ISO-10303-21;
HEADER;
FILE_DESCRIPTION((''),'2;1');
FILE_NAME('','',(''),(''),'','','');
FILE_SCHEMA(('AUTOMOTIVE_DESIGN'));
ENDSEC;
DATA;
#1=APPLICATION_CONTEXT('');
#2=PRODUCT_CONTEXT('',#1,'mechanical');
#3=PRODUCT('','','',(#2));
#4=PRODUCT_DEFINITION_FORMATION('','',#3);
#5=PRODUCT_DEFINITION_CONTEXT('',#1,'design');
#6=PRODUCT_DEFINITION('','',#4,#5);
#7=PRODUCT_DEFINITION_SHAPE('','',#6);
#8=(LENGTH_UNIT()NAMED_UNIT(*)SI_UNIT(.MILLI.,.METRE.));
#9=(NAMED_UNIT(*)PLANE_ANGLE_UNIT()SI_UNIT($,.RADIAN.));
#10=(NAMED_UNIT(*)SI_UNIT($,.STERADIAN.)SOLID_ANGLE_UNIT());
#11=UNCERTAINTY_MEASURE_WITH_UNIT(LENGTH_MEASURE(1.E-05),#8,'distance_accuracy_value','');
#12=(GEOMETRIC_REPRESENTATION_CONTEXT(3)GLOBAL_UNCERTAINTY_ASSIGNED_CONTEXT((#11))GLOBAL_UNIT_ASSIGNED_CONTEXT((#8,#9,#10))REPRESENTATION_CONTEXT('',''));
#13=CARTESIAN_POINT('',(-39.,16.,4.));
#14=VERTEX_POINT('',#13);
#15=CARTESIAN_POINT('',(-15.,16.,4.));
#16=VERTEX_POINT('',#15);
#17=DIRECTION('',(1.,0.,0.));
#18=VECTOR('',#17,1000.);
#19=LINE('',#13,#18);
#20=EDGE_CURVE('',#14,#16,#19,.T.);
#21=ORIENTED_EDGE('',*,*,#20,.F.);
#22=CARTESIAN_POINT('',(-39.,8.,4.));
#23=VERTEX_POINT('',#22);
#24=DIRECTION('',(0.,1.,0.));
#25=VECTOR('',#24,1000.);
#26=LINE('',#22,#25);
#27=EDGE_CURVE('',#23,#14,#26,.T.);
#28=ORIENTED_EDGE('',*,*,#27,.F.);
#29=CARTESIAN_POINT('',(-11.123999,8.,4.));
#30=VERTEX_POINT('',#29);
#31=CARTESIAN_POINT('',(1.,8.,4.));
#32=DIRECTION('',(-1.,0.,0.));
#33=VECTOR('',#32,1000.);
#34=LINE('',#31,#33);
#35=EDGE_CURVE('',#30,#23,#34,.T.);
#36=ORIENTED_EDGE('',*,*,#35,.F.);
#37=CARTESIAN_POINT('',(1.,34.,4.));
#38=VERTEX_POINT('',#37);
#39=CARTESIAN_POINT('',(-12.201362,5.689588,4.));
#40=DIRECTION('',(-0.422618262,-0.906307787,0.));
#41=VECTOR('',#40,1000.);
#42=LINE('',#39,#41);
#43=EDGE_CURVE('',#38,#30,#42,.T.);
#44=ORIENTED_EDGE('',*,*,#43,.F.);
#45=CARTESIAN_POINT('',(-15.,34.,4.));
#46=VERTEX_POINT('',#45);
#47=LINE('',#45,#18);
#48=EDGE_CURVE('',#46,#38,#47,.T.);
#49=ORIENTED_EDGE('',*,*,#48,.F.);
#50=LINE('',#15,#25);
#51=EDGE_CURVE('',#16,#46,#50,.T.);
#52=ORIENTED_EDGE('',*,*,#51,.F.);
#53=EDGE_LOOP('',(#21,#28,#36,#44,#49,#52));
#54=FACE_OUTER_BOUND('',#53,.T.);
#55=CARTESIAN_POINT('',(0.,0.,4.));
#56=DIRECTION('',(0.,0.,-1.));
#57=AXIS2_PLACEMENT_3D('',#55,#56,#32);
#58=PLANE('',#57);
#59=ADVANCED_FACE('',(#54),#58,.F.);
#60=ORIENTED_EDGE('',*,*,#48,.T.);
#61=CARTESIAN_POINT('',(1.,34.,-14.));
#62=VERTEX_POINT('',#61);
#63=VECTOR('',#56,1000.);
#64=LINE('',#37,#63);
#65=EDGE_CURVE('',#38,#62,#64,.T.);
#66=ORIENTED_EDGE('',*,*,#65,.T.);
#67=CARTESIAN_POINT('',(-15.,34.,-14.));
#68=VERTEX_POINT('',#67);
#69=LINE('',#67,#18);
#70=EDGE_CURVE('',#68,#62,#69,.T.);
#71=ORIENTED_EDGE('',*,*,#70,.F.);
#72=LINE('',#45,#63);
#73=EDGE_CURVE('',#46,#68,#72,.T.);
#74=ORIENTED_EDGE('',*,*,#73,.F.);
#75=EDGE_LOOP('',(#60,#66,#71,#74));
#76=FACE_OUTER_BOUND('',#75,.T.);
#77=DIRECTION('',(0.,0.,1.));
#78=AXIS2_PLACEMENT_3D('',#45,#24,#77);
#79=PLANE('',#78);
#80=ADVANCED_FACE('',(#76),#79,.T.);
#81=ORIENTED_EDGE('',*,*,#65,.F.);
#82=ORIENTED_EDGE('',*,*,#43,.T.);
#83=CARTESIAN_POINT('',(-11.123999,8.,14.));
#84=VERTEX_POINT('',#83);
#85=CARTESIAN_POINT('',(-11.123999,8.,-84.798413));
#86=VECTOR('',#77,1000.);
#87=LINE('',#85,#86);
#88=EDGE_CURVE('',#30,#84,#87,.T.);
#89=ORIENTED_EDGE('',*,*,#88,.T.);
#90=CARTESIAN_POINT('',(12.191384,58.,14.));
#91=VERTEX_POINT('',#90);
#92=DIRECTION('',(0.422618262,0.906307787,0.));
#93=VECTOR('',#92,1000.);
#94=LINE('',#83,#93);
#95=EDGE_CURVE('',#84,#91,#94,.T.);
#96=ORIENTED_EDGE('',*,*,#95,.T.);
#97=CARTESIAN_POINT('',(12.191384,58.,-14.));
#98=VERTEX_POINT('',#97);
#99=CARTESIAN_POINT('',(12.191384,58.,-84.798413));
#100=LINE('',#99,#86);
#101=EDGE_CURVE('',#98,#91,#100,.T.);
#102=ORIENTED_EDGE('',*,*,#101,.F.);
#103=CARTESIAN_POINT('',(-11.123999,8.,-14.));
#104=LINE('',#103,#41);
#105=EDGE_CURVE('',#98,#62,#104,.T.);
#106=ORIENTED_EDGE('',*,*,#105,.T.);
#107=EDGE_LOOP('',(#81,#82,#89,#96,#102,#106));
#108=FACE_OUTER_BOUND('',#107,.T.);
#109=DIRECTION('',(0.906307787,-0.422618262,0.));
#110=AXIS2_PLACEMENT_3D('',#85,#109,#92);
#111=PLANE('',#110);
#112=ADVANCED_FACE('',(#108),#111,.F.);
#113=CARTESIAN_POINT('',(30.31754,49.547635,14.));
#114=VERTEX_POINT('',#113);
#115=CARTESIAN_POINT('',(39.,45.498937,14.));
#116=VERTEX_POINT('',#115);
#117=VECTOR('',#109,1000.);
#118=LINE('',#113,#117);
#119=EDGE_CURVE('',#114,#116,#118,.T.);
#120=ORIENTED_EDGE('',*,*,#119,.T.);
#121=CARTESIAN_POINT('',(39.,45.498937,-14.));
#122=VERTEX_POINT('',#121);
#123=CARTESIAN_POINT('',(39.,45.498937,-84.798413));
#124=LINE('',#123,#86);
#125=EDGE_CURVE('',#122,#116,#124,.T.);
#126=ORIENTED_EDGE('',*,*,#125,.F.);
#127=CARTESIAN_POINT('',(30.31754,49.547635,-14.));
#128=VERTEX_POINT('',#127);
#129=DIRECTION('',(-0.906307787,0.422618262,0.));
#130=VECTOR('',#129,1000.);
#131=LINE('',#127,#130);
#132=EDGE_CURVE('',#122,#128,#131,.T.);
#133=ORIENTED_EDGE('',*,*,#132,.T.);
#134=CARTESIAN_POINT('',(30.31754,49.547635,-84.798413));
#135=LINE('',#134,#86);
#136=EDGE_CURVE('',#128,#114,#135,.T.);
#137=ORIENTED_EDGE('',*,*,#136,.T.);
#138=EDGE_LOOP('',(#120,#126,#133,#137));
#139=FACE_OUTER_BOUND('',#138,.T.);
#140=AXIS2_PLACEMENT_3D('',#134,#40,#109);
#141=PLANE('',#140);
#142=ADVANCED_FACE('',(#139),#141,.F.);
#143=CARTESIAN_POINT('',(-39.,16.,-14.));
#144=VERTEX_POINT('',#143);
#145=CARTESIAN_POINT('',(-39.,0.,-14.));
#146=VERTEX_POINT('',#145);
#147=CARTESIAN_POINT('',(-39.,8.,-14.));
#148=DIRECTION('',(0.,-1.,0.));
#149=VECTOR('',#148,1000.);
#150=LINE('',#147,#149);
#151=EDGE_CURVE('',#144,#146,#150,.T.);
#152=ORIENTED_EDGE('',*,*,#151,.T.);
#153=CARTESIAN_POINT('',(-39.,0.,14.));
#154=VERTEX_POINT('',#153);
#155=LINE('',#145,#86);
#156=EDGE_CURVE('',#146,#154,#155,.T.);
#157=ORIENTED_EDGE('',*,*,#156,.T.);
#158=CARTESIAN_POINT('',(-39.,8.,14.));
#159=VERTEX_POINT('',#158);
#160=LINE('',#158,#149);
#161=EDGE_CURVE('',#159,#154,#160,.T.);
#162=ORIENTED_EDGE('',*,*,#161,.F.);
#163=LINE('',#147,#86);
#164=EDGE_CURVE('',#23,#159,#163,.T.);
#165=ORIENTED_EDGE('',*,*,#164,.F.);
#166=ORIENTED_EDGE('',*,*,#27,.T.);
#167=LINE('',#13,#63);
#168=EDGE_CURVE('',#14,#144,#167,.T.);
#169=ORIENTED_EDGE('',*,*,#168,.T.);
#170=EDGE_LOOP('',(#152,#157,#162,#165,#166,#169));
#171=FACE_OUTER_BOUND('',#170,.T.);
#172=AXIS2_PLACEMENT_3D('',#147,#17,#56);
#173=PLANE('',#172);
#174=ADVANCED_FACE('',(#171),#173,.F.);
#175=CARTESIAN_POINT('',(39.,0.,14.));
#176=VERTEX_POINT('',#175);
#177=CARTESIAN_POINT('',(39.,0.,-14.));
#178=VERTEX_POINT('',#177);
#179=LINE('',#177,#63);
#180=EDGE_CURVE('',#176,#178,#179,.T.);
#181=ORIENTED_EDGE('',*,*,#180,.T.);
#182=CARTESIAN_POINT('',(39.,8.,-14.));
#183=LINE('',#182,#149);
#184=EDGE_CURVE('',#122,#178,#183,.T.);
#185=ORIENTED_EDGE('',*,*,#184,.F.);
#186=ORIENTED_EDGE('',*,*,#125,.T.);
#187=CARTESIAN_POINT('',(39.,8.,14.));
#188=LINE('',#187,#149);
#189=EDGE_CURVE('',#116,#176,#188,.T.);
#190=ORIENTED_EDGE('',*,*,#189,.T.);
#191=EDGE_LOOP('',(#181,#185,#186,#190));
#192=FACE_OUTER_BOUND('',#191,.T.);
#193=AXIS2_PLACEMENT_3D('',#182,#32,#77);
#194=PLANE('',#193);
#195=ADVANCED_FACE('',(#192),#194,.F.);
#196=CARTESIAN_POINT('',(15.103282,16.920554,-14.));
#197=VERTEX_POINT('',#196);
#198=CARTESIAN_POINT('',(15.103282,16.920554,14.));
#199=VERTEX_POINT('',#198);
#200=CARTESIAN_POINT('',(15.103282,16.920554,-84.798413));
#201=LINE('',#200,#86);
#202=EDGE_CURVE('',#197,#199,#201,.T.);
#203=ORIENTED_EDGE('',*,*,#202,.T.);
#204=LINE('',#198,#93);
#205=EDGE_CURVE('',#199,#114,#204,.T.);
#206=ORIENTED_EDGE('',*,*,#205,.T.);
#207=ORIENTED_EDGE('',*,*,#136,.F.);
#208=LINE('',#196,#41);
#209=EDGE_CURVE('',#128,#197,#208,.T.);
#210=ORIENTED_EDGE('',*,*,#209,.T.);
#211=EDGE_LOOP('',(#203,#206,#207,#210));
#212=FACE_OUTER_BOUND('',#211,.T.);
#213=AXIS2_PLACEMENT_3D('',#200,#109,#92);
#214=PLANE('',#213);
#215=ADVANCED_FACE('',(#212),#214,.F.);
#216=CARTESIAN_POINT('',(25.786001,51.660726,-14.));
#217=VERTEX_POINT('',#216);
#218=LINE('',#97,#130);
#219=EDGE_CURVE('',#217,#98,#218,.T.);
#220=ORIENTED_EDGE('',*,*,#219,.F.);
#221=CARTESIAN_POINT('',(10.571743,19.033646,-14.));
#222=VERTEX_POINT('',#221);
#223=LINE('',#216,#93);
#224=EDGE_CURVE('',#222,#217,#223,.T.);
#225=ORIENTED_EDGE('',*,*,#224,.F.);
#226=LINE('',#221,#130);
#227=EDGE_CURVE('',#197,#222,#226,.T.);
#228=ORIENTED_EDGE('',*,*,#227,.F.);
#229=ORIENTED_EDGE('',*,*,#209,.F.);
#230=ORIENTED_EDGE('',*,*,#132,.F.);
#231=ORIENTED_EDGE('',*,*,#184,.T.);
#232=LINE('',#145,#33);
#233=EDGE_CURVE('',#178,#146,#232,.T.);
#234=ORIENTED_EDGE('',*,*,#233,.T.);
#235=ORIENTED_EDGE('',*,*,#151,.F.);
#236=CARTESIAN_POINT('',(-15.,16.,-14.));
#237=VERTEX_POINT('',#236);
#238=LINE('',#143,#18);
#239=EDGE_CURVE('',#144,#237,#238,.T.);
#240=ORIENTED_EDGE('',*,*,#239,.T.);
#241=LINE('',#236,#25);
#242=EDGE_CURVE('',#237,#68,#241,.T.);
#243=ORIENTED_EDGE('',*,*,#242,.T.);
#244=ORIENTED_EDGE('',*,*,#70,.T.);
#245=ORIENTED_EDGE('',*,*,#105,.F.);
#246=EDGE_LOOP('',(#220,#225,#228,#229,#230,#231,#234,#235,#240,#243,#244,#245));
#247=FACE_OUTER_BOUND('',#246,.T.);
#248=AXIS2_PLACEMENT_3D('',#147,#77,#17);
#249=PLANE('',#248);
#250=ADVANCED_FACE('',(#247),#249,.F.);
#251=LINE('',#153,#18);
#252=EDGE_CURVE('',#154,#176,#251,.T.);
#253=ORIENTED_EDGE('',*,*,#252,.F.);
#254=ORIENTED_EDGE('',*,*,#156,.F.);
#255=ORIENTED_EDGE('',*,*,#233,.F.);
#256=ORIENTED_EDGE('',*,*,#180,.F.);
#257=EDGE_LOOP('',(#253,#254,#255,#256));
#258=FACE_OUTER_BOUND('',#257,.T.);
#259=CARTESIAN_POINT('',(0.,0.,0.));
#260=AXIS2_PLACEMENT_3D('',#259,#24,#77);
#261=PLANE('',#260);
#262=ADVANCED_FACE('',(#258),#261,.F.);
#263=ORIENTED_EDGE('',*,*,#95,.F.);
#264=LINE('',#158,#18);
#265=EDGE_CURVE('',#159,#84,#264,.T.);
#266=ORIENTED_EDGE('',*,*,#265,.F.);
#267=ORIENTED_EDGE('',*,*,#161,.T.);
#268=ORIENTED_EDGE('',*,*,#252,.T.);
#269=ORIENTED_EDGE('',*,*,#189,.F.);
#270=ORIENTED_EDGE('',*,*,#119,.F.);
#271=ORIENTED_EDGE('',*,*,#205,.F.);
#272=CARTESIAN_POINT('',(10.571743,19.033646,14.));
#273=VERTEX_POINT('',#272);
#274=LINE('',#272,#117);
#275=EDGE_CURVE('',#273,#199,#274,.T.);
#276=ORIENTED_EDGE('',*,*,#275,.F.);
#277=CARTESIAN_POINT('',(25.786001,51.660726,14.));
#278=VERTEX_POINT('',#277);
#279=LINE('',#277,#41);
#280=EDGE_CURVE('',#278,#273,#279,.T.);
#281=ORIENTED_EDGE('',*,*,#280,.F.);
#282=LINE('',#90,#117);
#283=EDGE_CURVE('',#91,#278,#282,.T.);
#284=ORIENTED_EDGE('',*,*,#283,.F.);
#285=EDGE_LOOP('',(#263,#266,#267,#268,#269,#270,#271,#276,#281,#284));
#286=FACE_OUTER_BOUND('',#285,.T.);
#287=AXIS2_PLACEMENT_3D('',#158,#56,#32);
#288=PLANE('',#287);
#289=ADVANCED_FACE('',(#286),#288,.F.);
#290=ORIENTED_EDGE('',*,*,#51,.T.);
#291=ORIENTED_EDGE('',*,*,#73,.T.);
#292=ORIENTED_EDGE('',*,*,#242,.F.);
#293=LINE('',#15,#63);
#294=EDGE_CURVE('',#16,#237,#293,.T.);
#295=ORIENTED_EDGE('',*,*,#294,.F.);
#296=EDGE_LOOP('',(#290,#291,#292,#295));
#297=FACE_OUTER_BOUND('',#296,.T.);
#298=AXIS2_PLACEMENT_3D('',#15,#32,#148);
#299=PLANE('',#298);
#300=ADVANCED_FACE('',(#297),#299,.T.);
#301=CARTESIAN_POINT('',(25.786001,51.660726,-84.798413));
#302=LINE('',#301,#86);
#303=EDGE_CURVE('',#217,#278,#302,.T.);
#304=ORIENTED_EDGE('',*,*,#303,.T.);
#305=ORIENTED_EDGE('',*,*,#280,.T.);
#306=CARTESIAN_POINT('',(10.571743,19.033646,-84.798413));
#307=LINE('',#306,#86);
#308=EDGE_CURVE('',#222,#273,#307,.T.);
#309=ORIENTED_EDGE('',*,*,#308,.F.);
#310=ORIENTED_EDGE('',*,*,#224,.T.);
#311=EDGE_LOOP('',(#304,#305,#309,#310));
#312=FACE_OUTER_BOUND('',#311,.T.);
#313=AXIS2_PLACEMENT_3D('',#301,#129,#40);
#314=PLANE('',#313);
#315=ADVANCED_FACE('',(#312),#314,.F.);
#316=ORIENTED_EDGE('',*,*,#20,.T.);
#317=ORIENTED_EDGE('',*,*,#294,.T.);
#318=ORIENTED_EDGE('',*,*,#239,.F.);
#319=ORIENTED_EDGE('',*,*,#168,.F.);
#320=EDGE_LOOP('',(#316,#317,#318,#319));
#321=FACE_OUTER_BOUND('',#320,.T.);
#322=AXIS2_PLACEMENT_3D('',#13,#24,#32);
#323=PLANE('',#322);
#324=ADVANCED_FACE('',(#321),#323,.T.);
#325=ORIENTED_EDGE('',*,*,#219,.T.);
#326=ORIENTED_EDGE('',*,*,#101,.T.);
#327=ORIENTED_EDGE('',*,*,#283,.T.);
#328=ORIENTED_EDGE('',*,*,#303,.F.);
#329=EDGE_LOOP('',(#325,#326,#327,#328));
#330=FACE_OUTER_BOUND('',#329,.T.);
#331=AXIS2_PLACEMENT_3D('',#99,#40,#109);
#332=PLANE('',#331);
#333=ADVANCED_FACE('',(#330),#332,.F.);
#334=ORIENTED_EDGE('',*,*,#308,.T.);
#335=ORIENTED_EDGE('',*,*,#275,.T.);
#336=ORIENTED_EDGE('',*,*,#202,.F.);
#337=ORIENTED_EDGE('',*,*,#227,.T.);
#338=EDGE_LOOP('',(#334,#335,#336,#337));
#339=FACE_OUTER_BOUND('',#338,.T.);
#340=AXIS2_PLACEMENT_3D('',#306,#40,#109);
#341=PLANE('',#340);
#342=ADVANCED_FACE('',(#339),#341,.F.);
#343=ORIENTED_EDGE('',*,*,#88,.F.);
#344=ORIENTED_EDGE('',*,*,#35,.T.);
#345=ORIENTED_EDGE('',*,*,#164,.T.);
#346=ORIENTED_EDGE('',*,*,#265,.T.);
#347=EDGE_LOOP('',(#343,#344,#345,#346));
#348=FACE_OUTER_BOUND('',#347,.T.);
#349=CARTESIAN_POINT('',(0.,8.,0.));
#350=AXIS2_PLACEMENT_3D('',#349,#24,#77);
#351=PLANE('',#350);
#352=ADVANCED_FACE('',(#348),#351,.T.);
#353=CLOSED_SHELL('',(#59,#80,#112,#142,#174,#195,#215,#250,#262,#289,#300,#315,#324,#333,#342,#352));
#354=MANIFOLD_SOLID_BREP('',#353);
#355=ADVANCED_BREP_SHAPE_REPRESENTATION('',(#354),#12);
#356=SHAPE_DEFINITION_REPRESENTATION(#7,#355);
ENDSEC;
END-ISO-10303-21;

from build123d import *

# Parameters (mm, degrees)
BASE_PLATE_SKETCH_W      = 78
BASE_PLATE_SKETCH_H      = 28
BASE_PLATE_78X28X8_DEPTH = 8
STEP_BLOCK_DEPTH         = 18
V_NOTCH_UPRIGHT_REACH    = 60.83


with BuildPart() as part:
    # Base Plate Sketch → Base Plate 78x28x8 (new body)
    with BuildSketch(Plane(origin=(0, 0, 0), x_dir=(1, 0, 0), z_dir=(0, 1, 0))):
        Rectangle(BASE_PLATE_SKETCH_W, BASE_PLATE_SKETCH_H)
    extrude(amount=BASE_PLATE_78X28X8_DEPTH)

    # Step Block Sketch → Step Block (add)
    with BuildSketch(Plane(origin=(0, 0, -14), x_dir=(-1, 0, 0), z_dir=(0, 0, -1))):
        Polygon((39, 8), (39, 16), (15, 16), (15, 34), (-1, 34), (-1, 8), align=None)
    extrude(amount=-STEP_BLOCK_DEPTH)

    # V-Notch Upright: up to this face of the body (flat: up to its plane)
    v_notch_upright_end = Plane(part.part.faces().sort_by_distance((-6.571428571, 10.987012987, -14))[0])
    # V-Notch Upright Sketch → V-Notch Upright (add, up to the picked face)
    with BuildSketch(Plane.XY.offset(14), mode=Mode.PRIVATE) as v_notch_upright_sk1:
        Polygon((-11.123999112, 8), (12.191383796, 58), (25.786000601, 51.660726074), (10.571743179, 19.033645741), (15.103282114, 16.920554432), (30.317539536, 49.547634765), (39, 45.498936959), (39, 8), align=None)
    v_notch_upright_tool1 = split(extrude(v_notch_upright_sk1.sketch, amount=-V_NOTCH_UPRIGHT_REACH, mode=Mode.PRIVATE), bisect_by=v_notch_upright_end, keep=Keep.BOTH, mode=Mode.PRIVATE)
    add(v_notch_upright_tool1.solids().sort_by(Axis((1.175344, 32.700793, 14), (0, 0, -1)))[0])


solid = part.part
